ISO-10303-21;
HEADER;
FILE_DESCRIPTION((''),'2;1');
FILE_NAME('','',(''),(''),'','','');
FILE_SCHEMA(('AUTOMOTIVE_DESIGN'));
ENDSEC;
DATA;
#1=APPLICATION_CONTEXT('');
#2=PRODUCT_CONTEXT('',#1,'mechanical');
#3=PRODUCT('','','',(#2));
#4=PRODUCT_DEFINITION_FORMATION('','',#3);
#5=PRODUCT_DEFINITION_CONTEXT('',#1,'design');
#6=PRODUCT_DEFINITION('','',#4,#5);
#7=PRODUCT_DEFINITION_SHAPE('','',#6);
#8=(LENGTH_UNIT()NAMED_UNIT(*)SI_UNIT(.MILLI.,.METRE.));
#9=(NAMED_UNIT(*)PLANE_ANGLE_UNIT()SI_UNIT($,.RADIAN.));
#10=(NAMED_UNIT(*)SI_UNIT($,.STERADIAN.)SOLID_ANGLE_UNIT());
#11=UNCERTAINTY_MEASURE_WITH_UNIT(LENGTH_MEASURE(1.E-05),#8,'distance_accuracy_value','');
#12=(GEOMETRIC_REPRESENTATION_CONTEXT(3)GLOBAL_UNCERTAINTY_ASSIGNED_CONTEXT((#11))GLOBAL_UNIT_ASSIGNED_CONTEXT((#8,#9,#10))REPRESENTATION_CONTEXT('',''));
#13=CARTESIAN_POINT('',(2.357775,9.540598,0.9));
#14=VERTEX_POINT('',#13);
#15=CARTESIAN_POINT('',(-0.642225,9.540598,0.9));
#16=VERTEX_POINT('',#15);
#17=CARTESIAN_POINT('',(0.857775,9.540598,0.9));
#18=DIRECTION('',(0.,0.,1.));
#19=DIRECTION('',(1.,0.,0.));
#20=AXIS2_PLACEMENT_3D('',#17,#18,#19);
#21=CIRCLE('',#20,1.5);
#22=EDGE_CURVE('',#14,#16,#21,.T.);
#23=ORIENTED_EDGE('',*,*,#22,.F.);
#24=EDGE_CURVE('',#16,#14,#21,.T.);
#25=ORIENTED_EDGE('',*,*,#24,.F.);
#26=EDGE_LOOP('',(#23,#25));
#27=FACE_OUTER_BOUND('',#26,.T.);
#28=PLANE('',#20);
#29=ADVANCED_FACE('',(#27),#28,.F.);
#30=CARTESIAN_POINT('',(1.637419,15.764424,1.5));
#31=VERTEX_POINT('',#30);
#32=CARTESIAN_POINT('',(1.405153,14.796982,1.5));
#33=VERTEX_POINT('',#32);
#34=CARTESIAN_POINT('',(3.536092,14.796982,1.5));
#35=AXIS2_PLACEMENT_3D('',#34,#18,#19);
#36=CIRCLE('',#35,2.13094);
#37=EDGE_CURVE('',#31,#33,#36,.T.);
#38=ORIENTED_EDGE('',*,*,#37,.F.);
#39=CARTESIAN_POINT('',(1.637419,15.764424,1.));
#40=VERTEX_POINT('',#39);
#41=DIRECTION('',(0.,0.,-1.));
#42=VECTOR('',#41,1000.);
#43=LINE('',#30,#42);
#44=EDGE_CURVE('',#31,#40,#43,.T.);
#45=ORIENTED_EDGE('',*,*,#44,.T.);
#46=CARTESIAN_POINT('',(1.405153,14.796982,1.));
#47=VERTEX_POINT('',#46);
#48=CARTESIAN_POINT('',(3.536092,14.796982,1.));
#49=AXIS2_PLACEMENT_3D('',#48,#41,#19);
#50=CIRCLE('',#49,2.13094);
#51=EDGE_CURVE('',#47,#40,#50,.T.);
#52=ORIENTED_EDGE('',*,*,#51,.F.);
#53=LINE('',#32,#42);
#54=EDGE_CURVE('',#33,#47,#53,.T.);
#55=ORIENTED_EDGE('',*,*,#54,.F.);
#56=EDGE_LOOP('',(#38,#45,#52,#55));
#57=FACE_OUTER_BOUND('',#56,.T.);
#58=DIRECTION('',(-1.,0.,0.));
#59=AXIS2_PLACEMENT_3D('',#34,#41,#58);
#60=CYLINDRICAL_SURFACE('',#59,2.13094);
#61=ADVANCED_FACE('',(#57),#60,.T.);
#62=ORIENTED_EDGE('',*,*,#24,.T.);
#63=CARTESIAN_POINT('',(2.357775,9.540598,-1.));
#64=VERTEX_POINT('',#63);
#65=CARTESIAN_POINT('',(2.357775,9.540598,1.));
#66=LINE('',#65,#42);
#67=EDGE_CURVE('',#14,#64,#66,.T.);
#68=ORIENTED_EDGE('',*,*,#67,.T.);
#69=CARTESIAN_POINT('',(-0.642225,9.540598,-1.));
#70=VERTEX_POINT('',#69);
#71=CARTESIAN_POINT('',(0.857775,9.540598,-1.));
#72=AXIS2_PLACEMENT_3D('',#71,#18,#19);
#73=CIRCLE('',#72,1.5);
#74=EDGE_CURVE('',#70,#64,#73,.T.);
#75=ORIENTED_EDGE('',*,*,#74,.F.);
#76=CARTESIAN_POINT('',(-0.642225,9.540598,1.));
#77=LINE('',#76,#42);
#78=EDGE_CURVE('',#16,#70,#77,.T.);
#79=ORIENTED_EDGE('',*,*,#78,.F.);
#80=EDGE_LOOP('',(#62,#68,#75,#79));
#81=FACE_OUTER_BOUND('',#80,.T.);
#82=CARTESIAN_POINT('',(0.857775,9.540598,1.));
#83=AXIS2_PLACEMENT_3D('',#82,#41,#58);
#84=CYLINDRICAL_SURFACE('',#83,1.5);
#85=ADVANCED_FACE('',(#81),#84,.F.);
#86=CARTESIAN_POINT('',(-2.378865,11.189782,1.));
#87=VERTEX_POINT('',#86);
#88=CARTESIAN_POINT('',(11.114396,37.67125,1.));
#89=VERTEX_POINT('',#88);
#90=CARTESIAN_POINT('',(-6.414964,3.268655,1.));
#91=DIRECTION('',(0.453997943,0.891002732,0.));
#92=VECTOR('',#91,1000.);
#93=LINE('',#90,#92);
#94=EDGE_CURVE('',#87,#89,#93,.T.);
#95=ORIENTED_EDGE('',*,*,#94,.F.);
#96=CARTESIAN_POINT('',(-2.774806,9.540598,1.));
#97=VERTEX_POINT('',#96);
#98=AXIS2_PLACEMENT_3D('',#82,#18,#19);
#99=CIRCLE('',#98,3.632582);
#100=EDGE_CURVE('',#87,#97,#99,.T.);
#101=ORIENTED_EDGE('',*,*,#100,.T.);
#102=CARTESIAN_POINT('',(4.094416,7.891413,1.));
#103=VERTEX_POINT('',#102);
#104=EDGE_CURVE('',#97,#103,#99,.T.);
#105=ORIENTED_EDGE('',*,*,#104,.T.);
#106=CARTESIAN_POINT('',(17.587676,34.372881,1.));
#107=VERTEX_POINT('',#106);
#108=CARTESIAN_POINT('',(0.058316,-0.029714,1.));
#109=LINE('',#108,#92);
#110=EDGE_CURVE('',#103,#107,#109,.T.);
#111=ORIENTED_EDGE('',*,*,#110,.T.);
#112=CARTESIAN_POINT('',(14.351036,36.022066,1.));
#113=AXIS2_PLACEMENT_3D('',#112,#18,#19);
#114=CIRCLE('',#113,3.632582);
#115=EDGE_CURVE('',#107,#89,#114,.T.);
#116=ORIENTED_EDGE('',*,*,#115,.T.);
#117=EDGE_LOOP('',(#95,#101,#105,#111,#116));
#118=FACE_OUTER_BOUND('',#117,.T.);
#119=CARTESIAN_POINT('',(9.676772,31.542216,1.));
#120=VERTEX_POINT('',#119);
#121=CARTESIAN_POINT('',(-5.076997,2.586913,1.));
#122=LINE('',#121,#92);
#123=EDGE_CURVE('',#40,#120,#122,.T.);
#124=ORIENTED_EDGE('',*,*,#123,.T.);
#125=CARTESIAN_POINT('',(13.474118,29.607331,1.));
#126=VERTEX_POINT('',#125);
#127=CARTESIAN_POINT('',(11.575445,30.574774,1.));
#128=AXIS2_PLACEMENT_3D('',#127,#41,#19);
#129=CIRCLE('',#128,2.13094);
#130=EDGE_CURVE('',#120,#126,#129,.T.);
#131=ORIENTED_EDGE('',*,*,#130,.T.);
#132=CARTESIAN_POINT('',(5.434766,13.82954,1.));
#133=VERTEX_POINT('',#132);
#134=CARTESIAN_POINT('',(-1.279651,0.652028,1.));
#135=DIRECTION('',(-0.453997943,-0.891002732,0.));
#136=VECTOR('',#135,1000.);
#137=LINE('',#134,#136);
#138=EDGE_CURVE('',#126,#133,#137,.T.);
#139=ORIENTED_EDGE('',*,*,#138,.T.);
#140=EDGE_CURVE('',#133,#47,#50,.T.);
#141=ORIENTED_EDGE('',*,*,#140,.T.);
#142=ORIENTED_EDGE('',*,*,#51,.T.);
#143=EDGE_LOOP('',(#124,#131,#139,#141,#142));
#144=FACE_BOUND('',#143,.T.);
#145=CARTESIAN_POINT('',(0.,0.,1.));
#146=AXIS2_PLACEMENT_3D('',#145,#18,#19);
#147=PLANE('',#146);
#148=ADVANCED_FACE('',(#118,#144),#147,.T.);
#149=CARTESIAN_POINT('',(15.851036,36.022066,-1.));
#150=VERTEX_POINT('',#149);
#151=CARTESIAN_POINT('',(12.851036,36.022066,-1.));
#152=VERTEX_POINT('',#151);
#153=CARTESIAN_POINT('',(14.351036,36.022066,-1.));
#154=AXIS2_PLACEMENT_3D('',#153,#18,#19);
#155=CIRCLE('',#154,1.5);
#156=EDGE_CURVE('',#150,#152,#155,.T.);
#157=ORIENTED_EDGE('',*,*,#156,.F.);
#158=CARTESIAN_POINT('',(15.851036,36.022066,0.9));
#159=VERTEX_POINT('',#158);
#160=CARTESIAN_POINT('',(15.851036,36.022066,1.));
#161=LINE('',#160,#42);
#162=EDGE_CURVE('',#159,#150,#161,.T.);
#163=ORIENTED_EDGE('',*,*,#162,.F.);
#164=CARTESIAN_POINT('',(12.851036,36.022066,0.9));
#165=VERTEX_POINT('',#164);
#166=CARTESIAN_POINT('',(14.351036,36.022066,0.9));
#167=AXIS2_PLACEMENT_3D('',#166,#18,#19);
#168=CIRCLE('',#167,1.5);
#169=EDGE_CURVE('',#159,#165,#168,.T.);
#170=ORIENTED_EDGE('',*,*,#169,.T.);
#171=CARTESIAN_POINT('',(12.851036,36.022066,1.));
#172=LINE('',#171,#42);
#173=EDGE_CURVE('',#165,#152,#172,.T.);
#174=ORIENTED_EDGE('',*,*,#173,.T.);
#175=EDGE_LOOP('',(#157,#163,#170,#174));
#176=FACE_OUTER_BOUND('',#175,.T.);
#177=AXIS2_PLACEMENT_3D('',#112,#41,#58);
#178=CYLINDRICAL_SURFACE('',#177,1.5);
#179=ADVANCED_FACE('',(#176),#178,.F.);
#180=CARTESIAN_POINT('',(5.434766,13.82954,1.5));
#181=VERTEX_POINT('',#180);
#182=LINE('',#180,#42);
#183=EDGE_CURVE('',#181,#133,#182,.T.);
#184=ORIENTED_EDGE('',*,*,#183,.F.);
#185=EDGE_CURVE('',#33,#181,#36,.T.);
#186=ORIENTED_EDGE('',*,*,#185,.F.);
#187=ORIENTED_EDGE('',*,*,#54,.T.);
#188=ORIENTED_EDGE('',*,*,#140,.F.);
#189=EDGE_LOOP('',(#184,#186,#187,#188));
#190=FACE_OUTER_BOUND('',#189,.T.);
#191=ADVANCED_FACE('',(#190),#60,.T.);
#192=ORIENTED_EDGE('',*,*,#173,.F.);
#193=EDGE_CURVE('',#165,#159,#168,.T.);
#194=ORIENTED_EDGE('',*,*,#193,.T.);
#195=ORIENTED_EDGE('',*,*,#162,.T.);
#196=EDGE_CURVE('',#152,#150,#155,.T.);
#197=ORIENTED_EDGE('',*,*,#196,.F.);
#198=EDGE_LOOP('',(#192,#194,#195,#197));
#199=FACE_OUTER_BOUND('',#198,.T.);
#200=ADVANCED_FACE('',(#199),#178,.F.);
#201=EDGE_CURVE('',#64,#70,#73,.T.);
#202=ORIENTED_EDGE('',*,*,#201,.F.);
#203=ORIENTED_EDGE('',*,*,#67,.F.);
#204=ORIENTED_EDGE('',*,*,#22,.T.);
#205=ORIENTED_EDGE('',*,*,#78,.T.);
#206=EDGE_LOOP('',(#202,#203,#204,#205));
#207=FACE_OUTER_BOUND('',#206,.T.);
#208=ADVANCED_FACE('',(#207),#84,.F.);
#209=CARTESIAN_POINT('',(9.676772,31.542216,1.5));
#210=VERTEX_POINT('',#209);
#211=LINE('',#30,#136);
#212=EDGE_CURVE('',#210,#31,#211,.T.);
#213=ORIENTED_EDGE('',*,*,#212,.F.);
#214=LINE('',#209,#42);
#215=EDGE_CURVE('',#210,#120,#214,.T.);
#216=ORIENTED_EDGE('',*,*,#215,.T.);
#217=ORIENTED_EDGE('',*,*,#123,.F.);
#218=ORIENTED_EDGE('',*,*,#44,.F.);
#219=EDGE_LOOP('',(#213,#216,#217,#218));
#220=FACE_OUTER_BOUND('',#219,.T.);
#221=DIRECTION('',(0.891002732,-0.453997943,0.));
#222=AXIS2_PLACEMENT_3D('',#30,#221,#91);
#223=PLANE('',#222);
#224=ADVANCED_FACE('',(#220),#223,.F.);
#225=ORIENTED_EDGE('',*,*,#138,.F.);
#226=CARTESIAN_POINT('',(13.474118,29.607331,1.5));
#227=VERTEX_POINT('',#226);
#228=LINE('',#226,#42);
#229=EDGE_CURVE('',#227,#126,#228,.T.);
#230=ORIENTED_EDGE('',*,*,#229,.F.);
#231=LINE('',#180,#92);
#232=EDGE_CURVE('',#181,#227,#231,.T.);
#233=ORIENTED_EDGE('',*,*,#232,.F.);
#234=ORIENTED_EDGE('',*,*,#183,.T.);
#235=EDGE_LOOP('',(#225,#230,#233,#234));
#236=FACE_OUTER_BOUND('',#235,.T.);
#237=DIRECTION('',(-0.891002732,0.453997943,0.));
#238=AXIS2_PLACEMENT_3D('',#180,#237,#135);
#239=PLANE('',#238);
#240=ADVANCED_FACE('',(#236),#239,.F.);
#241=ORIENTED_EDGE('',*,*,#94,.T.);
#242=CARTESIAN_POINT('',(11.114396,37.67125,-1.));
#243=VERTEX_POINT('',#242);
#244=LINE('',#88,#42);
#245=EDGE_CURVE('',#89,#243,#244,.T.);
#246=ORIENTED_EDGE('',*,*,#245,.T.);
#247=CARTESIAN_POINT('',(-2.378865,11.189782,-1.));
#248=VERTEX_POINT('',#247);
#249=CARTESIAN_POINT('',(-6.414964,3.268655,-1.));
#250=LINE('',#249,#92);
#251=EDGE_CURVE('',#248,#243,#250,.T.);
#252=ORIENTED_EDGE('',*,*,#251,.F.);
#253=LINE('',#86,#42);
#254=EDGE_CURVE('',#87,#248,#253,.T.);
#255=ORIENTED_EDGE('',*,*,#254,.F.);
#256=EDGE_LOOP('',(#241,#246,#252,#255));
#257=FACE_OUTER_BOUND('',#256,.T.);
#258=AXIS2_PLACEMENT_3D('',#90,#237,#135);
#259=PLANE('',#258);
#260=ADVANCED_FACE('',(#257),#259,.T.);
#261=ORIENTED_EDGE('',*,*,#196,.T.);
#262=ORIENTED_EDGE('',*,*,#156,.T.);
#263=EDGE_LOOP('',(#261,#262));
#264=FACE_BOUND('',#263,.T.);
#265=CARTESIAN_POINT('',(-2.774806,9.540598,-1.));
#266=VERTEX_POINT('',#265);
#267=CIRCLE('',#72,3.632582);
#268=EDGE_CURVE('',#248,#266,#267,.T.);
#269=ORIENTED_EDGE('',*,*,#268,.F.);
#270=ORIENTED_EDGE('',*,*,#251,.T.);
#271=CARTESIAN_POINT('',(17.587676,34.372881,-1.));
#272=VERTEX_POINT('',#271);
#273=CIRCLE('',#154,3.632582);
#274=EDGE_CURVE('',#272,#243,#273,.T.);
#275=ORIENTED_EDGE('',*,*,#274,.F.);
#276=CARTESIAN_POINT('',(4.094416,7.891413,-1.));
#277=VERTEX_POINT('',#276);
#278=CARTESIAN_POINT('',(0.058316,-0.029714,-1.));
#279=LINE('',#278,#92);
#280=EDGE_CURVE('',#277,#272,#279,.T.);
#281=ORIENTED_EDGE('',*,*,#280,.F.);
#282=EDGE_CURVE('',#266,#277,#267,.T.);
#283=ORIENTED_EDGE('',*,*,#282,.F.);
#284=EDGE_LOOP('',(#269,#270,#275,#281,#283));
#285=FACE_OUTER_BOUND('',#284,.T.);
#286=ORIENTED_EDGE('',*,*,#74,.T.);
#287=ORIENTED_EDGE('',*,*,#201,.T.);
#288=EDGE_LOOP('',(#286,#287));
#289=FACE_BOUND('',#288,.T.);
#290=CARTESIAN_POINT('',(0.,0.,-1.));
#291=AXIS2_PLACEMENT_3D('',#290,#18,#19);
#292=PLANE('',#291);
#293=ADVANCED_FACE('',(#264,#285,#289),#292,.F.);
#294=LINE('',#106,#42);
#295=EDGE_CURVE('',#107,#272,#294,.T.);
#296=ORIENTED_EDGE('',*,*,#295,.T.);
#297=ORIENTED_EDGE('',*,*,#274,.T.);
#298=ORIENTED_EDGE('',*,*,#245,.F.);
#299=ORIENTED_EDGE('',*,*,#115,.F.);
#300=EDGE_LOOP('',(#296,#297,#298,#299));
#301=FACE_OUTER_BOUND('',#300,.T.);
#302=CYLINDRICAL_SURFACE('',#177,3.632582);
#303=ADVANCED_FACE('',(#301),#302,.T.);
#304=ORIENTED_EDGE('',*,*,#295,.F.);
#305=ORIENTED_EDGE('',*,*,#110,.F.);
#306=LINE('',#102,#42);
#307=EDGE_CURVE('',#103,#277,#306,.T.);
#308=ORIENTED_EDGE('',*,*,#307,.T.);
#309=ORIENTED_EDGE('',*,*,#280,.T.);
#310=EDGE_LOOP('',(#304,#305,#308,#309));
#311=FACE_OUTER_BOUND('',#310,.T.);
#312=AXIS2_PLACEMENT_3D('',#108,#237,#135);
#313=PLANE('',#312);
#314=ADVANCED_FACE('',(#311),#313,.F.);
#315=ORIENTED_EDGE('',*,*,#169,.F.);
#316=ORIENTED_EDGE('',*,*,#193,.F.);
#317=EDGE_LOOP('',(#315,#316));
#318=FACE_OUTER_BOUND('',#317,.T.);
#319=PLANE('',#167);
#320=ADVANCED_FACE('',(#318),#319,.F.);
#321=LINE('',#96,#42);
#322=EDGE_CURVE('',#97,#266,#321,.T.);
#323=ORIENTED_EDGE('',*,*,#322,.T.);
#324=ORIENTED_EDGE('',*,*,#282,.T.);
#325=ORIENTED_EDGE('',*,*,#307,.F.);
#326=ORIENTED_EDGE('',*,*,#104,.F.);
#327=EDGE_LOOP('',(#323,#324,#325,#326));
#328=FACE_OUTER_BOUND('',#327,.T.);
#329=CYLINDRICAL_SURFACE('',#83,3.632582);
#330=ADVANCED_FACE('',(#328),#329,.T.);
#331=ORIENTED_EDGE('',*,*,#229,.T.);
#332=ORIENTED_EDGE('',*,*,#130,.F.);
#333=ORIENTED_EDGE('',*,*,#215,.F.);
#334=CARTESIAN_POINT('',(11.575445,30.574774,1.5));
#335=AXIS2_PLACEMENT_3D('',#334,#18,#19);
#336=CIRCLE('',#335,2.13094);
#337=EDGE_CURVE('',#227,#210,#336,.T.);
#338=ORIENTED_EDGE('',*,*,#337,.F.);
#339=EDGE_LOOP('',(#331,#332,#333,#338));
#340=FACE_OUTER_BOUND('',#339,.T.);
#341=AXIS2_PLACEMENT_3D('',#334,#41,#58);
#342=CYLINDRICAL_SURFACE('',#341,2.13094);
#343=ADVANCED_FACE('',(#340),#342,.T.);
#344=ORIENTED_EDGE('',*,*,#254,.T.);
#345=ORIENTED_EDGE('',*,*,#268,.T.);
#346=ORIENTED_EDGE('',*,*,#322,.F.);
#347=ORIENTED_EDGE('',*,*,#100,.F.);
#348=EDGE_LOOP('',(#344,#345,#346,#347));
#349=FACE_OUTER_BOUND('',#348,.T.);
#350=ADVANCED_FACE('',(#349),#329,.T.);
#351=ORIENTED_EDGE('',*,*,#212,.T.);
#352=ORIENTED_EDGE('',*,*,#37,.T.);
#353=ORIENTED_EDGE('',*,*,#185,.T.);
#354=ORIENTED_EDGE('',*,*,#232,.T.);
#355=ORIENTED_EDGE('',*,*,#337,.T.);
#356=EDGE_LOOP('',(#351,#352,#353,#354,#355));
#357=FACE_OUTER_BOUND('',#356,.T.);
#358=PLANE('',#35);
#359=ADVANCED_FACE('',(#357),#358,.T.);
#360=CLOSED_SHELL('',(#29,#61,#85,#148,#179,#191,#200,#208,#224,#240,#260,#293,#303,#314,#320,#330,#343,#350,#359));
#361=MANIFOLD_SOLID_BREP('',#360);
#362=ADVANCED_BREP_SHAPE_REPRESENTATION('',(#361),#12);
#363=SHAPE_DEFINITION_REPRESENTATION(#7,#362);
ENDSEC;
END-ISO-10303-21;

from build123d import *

# Parameters (mm, degrees)
SKETCH2_R           = 1.5
BOSS_EXTRUDE1_DEPTH = 1
BOSS_EXTRUDE2_DEPTH = 0.5
BOSS_EXTRUDE3_START = -0.1
SKETCH4_R           = 1.5
BOSS_EXTRUDE3_DEPTH = 0.1
BOSS_EXTRUDE5_START = -0.1
SKETCH5_R           = 1.5
BOSS_EXTRUDE5_DEPTH = 0.1


with BuildPart() as part:
    # Sketch2 → Boss-Extrude1 (new, symmetric)
    with BuildSketch(Plane.XY):
        with BuildLine():
            Line((-2.378864653, 11.189782176), (11.114395932, 37.671250283))
            ThreePointArc((11.114395932, 37.671250283), (16.00022062, 39.258705834), (17.587676171, 34.372881146))
            Line((17.587676171, 34.372881146), (4.094415586, 7.891413039))
            ThreePointArc((4.094415586, 7.891413039), (-0.791409102, 6.303957488), (-2.378864653, 11.189782176))
        make_face()
        with Locations((0.857775466, 9.540597607)):
            Circle(SKETCH2_R, mode=Mode.SUBTRACT)
        with Locations((14.351036052, 36.022065714)):
            Circle(SKETCH2_R, mode=Mode.SUBTRACT)
    extrude(amount=BOSS_EXTRUDE1_DEPTH, both=True)

    # Sketch3 → Boss-Extrude2 (add, symmetric)
    with BuildSketch(Plane.XY.offset(1)):
        with BuildLine():
            Line((1.637419261, 15.764424462), (9.676771623, 31.542216036))
            ThreePointArc((9.676771623, 31.542216036), (12.542887141, 32.47344695), (13.474118055, 29.607331431))
            Line((13.474118055, 29.607331431), (5.434765693, 13.829539858))
            ThreePointArc((5.434765693, 13.829539858), (2.568650175, 12.898308944), (1.637419261, 15.764424462))
        make_face()
    extrude(amount=BOSS_EXTRUDE2_DEPTH, both=True)

    # Sketch4 → Boss-Extrude3 (add)
    with BuildSketch(Plane.XY.offset(1).offset(BOSS_EXTRUDE3_START)):
        with Locations((0.857775466, 9.540597607)):
            Circle(SKETCH4_R)
    extrude(amount=BOSS_EXTRUDE3_DEPTH)

    # Sketch5 → Boss-Extrude5 (add)
    with BuildSketch(Plane.XY.offset(1).offset(BOSS_EXTRUDE5_START)):
        with Locations((14.351036052, 36.022065714)):
            Circle(SKETCH5_R)
    extrude(amount=BOSS_EXTRUDE5_DEPTH)


solid = part.part
